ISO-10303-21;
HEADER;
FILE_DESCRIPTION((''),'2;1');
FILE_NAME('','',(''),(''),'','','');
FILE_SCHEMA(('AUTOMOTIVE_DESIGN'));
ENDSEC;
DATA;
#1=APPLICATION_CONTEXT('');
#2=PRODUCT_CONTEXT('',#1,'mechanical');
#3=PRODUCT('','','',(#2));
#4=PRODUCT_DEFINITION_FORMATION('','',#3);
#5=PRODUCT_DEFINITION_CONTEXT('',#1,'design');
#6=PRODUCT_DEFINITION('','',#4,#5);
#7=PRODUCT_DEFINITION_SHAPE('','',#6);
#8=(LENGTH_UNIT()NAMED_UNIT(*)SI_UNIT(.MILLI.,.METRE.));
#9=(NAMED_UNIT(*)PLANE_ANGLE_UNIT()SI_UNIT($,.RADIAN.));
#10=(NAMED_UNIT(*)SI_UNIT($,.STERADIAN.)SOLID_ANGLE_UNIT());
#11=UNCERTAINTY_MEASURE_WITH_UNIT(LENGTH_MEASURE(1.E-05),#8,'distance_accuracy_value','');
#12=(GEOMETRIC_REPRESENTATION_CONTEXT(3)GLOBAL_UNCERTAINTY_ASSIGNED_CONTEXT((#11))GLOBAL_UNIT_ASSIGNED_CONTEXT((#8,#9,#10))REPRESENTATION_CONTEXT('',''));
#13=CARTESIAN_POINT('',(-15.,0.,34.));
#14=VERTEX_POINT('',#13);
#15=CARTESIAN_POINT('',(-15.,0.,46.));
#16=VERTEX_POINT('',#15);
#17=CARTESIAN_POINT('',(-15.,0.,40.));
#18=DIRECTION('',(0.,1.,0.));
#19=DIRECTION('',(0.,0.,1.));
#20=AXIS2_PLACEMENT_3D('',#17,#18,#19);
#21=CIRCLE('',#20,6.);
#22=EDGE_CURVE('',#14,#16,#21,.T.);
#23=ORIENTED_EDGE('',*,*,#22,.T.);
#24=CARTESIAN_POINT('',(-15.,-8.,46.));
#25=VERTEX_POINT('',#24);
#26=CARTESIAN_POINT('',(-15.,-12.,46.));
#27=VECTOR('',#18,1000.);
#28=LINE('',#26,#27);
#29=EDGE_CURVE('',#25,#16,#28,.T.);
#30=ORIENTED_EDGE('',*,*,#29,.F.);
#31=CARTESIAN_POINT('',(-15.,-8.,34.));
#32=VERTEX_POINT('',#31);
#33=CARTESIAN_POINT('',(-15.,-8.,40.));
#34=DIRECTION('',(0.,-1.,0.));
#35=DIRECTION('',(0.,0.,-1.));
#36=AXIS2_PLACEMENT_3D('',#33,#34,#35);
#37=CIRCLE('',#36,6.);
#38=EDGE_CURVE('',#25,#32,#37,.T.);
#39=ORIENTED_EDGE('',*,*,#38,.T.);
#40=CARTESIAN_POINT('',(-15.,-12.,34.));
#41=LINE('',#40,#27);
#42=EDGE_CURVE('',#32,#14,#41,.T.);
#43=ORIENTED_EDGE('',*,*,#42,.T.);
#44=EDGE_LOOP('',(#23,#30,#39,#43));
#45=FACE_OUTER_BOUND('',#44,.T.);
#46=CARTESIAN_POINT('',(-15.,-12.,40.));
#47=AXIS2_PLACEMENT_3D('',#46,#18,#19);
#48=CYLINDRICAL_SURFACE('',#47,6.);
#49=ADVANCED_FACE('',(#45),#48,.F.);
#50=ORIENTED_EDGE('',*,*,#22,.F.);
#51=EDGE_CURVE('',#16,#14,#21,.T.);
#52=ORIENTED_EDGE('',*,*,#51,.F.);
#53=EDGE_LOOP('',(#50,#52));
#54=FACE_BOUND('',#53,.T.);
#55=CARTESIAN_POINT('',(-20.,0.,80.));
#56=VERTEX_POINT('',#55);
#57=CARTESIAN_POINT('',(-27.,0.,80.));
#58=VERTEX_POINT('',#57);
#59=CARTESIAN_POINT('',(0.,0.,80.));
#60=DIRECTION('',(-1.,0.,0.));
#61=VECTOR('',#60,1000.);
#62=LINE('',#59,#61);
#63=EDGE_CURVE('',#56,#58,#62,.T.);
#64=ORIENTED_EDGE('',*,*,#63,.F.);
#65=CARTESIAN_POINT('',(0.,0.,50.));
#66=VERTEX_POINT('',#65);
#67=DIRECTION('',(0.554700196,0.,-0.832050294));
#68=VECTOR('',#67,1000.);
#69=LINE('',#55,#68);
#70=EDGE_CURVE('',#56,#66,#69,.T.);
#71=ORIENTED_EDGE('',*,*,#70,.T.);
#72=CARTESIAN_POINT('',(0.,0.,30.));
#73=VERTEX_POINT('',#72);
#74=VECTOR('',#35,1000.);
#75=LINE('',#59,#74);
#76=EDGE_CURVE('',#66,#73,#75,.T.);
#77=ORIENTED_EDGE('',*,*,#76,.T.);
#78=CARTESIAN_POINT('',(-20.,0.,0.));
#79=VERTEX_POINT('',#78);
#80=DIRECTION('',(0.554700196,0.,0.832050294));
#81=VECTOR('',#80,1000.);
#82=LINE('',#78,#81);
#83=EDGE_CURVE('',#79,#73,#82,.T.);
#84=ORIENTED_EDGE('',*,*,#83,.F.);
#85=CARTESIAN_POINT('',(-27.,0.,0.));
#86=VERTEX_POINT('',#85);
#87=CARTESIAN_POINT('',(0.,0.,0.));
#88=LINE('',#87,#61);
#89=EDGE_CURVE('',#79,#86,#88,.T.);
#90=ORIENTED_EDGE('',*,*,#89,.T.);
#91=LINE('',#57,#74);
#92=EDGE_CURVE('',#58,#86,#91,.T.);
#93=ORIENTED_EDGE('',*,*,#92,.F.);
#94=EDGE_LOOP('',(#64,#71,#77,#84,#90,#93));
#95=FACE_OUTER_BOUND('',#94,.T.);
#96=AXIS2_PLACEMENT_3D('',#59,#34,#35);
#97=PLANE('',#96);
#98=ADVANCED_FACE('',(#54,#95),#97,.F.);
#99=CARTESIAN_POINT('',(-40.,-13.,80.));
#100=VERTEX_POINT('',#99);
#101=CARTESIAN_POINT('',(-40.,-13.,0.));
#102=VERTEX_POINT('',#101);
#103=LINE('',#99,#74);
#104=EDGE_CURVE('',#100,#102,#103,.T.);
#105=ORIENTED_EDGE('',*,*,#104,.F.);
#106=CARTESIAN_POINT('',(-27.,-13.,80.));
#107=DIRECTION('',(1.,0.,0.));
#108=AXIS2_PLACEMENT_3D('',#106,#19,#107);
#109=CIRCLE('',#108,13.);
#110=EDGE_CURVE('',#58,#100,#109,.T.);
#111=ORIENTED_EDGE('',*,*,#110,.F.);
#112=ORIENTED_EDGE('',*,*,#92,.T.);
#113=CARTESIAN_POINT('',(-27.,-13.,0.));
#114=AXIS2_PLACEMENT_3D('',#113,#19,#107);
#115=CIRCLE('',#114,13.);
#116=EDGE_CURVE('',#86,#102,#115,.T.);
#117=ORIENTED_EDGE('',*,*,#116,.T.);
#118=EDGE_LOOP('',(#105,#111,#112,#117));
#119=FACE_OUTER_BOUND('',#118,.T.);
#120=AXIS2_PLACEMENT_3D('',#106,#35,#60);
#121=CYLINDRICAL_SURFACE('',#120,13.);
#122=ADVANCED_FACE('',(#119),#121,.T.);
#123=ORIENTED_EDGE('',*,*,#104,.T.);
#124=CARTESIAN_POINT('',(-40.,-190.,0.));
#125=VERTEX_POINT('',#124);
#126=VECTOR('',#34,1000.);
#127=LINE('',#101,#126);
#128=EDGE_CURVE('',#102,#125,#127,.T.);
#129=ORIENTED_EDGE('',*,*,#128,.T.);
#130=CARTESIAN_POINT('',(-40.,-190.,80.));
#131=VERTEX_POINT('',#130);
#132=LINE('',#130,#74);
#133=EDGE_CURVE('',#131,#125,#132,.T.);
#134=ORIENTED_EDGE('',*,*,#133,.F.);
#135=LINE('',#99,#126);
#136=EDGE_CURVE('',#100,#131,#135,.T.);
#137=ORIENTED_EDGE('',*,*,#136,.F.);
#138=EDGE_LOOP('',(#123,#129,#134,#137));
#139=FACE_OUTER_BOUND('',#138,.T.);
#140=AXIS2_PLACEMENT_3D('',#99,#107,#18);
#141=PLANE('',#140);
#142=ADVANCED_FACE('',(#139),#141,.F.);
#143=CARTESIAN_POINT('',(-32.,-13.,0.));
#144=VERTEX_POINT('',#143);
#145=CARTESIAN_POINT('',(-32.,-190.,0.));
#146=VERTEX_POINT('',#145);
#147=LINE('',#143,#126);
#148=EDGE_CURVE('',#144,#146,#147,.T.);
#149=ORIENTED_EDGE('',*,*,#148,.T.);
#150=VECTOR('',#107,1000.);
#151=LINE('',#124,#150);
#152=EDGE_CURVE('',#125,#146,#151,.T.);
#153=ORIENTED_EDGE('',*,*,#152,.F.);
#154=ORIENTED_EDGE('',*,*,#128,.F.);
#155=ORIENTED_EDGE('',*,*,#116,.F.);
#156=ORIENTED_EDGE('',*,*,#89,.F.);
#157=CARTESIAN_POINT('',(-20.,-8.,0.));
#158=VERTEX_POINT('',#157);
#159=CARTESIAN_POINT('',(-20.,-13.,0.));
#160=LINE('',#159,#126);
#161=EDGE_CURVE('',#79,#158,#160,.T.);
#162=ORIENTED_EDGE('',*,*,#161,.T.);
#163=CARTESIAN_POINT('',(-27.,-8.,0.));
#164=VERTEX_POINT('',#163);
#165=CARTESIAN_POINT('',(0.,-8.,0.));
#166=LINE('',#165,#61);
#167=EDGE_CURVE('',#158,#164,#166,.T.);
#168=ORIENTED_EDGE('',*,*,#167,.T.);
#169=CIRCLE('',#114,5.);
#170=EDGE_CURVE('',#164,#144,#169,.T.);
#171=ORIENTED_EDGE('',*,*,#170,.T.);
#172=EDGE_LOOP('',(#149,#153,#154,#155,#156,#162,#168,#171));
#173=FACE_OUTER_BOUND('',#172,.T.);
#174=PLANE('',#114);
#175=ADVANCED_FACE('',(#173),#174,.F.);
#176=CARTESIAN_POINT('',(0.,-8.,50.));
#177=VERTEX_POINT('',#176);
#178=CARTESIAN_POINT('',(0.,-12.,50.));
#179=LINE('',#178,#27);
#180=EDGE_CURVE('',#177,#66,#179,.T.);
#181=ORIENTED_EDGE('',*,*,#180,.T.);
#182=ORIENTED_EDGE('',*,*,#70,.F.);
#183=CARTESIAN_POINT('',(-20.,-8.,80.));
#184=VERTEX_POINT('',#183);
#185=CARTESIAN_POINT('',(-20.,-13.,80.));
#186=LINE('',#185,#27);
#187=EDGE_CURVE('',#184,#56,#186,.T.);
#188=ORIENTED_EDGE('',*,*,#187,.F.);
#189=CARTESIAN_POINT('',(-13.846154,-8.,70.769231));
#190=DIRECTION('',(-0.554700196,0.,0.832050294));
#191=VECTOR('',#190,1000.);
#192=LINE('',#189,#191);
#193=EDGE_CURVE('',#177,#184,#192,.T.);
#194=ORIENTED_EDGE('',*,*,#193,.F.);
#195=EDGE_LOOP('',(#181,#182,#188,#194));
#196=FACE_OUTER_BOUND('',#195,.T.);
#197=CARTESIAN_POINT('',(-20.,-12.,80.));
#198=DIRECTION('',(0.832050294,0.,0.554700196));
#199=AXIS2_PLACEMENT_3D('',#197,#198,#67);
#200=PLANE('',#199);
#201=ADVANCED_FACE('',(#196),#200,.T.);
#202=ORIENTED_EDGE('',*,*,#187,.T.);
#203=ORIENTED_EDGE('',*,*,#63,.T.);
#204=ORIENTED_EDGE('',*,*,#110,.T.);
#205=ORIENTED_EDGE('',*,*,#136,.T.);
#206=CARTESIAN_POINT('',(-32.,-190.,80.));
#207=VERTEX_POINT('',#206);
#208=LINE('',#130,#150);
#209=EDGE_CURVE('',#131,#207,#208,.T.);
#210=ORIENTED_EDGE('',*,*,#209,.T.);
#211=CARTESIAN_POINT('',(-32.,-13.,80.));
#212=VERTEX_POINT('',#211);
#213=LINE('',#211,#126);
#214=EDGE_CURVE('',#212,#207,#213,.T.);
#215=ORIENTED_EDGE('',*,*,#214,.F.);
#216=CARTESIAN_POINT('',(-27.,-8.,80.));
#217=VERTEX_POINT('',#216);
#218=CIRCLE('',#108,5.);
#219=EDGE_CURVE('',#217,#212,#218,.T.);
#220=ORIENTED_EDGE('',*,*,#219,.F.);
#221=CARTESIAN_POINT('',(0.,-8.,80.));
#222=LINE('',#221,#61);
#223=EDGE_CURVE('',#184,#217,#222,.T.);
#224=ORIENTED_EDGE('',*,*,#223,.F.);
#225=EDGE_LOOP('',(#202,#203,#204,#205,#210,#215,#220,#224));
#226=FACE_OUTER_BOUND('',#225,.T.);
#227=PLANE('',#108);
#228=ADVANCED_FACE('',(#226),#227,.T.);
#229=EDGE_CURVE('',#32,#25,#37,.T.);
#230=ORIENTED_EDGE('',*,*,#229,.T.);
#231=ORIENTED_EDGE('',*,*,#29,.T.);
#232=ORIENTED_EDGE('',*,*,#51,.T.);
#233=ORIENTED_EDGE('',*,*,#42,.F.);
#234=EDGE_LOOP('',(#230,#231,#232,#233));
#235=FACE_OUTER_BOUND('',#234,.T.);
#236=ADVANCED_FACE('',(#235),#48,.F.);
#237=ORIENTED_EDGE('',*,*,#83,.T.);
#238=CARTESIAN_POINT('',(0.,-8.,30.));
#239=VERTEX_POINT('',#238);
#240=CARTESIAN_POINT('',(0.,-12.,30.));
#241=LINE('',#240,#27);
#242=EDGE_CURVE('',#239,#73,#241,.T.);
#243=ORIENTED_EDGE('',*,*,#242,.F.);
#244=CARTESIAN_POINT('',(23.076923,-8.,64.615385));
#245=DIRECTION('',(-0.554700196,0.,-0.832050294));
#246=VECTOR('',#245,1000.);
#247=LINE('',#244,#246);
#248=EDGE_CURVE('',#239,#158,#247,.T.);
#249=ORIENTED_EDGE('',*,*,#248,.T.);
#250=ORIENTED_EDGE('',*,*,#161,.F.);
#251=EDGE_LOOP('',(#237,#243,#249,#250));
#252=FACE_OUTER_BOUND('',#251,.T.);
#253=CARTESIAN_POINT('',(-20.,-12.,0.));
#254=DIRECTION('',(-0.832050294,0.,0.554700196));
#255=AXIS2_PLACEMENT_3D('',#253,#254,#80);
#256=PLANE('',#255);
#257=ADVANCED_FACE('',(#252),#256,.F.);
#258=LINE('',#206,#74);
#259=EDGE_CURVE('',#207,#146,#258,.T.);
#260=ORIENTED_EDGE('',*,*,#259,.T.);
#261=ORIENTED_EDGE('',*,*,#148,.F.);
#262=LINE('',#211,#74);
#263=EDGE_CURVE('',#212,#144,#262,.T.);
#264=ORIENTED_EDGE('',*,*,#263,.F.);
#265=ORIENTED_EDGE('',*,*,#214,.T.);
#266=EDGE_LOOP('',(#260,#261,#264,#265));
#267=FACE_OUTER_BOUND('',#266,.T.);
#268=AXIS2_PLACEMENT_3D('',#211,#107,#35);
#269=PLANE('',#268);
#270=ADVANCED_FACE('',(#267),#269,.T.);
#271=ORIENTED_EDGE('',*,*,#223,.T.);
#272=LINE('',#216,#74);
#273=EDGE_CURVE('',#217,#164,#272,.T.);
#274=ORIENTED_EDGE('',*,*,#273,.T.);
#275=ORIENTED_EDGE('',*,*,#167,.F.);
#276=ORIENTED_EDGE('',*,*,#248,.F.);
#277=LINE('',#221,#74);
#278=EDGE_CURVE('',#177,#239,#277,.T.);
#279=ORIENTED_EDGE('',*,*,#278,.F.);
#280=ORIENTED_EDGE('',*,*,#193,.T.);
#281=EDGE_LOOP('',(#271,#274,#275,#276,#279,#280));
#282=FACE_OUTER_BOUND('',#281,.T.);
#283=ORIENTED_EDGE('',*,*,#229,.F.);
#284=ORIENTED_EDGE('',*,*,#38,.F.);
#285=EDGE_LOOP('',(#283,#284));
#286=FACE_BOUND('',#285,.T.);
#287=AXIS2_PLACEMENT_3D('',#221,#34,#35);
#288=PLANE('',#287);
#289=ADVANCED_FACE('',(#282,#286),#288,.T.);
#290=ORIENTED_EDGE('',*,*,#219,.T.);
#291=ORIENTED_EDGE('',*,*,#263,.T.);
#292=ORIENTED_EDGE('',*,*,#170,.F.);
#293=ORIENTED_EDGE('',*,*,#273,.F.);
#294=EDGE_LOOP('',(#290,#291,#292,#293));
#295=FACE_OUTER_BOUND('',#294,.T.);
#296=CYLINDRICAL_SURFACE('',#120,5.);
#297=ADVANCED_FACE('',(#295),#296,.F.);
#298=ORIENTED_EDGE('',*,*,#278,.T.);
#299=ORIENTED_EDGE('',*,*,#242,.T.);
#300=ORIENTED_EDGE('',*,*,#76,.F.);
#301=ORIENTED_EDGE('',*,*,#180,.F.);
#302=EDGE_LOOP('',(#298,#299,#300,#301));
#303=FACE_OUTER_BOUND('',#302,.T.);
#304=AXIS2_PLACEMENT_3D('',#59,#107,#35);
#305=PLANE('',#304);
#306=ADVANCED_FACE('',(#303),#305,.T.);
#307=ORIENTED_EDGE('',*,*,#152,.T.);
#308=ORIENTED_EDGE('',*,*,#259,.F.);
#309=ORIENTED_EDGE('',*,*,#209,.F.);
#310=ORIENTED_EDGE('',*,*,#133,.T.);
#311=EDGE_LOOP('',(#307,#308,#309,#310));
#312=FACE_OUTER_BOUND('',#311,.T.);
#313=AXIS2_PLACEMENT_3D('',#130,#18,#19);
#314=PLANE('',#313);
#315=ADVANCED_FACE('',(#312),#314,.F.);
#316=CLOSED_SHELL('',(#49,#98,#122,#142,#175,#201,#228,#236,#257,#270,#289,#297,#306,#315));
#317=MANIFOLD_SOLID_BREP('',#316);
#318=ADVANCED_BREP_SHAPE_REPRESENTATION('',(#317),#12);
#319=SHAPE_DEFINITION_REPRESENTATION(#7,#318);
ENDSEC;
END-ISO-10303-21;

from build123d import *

# Parameters (mm, degrees)
BOSS_EXTRUDE1_DEPTH = 80
SKETCH2_R           = 6
CUT_EXTRUDE1_DEPTH  = 12


with BuildPart() as part:
    # Sketch1 → Boss-Extrude1 (new body)
    with BuildSketch(Plane.XY):
        with BuildLine():
            Line((0, 0), (-27, 0))
            ThreePointArc((-27, 0), (-36.192388155, -3.807611845), (-40, -13))
            Line((-40, -13), (-40, -190))
            Line((-40, -190), (-32, -190))
            Line((-32, -190), (-32, -13))
            ThreePointArc((-32, -13), (-30.535533906, -9.464466094), (-27, -8))
            Line((-27, -8), (0, -8))
            Line((0, -8), (0, 0))
        make_face()
    extrude(amount=BOSS_EXTRUDE1_DEPTH)

    # Sketch2 → Cut-Extrude1 (cut)
    with BuildSketch(Plane(origin=(0, 0, 0), x_dir=(1, 0, 0), z_dir=(0, 1, 0))):
        with Locations(Location((-15, -40, 0), (0, 0, 270))):
            Circle(SKETCH2_R)
        Polygon((-20, 0), (0, -30), (0, 0), align=None)
        Polygon((0, -50), (0, -80), (-20, -80), align=None)
    extrude(amount=-CUT_EXTRUDE1_DEPTH, mode=Mode.SUBTRACT)


solid = part.part
